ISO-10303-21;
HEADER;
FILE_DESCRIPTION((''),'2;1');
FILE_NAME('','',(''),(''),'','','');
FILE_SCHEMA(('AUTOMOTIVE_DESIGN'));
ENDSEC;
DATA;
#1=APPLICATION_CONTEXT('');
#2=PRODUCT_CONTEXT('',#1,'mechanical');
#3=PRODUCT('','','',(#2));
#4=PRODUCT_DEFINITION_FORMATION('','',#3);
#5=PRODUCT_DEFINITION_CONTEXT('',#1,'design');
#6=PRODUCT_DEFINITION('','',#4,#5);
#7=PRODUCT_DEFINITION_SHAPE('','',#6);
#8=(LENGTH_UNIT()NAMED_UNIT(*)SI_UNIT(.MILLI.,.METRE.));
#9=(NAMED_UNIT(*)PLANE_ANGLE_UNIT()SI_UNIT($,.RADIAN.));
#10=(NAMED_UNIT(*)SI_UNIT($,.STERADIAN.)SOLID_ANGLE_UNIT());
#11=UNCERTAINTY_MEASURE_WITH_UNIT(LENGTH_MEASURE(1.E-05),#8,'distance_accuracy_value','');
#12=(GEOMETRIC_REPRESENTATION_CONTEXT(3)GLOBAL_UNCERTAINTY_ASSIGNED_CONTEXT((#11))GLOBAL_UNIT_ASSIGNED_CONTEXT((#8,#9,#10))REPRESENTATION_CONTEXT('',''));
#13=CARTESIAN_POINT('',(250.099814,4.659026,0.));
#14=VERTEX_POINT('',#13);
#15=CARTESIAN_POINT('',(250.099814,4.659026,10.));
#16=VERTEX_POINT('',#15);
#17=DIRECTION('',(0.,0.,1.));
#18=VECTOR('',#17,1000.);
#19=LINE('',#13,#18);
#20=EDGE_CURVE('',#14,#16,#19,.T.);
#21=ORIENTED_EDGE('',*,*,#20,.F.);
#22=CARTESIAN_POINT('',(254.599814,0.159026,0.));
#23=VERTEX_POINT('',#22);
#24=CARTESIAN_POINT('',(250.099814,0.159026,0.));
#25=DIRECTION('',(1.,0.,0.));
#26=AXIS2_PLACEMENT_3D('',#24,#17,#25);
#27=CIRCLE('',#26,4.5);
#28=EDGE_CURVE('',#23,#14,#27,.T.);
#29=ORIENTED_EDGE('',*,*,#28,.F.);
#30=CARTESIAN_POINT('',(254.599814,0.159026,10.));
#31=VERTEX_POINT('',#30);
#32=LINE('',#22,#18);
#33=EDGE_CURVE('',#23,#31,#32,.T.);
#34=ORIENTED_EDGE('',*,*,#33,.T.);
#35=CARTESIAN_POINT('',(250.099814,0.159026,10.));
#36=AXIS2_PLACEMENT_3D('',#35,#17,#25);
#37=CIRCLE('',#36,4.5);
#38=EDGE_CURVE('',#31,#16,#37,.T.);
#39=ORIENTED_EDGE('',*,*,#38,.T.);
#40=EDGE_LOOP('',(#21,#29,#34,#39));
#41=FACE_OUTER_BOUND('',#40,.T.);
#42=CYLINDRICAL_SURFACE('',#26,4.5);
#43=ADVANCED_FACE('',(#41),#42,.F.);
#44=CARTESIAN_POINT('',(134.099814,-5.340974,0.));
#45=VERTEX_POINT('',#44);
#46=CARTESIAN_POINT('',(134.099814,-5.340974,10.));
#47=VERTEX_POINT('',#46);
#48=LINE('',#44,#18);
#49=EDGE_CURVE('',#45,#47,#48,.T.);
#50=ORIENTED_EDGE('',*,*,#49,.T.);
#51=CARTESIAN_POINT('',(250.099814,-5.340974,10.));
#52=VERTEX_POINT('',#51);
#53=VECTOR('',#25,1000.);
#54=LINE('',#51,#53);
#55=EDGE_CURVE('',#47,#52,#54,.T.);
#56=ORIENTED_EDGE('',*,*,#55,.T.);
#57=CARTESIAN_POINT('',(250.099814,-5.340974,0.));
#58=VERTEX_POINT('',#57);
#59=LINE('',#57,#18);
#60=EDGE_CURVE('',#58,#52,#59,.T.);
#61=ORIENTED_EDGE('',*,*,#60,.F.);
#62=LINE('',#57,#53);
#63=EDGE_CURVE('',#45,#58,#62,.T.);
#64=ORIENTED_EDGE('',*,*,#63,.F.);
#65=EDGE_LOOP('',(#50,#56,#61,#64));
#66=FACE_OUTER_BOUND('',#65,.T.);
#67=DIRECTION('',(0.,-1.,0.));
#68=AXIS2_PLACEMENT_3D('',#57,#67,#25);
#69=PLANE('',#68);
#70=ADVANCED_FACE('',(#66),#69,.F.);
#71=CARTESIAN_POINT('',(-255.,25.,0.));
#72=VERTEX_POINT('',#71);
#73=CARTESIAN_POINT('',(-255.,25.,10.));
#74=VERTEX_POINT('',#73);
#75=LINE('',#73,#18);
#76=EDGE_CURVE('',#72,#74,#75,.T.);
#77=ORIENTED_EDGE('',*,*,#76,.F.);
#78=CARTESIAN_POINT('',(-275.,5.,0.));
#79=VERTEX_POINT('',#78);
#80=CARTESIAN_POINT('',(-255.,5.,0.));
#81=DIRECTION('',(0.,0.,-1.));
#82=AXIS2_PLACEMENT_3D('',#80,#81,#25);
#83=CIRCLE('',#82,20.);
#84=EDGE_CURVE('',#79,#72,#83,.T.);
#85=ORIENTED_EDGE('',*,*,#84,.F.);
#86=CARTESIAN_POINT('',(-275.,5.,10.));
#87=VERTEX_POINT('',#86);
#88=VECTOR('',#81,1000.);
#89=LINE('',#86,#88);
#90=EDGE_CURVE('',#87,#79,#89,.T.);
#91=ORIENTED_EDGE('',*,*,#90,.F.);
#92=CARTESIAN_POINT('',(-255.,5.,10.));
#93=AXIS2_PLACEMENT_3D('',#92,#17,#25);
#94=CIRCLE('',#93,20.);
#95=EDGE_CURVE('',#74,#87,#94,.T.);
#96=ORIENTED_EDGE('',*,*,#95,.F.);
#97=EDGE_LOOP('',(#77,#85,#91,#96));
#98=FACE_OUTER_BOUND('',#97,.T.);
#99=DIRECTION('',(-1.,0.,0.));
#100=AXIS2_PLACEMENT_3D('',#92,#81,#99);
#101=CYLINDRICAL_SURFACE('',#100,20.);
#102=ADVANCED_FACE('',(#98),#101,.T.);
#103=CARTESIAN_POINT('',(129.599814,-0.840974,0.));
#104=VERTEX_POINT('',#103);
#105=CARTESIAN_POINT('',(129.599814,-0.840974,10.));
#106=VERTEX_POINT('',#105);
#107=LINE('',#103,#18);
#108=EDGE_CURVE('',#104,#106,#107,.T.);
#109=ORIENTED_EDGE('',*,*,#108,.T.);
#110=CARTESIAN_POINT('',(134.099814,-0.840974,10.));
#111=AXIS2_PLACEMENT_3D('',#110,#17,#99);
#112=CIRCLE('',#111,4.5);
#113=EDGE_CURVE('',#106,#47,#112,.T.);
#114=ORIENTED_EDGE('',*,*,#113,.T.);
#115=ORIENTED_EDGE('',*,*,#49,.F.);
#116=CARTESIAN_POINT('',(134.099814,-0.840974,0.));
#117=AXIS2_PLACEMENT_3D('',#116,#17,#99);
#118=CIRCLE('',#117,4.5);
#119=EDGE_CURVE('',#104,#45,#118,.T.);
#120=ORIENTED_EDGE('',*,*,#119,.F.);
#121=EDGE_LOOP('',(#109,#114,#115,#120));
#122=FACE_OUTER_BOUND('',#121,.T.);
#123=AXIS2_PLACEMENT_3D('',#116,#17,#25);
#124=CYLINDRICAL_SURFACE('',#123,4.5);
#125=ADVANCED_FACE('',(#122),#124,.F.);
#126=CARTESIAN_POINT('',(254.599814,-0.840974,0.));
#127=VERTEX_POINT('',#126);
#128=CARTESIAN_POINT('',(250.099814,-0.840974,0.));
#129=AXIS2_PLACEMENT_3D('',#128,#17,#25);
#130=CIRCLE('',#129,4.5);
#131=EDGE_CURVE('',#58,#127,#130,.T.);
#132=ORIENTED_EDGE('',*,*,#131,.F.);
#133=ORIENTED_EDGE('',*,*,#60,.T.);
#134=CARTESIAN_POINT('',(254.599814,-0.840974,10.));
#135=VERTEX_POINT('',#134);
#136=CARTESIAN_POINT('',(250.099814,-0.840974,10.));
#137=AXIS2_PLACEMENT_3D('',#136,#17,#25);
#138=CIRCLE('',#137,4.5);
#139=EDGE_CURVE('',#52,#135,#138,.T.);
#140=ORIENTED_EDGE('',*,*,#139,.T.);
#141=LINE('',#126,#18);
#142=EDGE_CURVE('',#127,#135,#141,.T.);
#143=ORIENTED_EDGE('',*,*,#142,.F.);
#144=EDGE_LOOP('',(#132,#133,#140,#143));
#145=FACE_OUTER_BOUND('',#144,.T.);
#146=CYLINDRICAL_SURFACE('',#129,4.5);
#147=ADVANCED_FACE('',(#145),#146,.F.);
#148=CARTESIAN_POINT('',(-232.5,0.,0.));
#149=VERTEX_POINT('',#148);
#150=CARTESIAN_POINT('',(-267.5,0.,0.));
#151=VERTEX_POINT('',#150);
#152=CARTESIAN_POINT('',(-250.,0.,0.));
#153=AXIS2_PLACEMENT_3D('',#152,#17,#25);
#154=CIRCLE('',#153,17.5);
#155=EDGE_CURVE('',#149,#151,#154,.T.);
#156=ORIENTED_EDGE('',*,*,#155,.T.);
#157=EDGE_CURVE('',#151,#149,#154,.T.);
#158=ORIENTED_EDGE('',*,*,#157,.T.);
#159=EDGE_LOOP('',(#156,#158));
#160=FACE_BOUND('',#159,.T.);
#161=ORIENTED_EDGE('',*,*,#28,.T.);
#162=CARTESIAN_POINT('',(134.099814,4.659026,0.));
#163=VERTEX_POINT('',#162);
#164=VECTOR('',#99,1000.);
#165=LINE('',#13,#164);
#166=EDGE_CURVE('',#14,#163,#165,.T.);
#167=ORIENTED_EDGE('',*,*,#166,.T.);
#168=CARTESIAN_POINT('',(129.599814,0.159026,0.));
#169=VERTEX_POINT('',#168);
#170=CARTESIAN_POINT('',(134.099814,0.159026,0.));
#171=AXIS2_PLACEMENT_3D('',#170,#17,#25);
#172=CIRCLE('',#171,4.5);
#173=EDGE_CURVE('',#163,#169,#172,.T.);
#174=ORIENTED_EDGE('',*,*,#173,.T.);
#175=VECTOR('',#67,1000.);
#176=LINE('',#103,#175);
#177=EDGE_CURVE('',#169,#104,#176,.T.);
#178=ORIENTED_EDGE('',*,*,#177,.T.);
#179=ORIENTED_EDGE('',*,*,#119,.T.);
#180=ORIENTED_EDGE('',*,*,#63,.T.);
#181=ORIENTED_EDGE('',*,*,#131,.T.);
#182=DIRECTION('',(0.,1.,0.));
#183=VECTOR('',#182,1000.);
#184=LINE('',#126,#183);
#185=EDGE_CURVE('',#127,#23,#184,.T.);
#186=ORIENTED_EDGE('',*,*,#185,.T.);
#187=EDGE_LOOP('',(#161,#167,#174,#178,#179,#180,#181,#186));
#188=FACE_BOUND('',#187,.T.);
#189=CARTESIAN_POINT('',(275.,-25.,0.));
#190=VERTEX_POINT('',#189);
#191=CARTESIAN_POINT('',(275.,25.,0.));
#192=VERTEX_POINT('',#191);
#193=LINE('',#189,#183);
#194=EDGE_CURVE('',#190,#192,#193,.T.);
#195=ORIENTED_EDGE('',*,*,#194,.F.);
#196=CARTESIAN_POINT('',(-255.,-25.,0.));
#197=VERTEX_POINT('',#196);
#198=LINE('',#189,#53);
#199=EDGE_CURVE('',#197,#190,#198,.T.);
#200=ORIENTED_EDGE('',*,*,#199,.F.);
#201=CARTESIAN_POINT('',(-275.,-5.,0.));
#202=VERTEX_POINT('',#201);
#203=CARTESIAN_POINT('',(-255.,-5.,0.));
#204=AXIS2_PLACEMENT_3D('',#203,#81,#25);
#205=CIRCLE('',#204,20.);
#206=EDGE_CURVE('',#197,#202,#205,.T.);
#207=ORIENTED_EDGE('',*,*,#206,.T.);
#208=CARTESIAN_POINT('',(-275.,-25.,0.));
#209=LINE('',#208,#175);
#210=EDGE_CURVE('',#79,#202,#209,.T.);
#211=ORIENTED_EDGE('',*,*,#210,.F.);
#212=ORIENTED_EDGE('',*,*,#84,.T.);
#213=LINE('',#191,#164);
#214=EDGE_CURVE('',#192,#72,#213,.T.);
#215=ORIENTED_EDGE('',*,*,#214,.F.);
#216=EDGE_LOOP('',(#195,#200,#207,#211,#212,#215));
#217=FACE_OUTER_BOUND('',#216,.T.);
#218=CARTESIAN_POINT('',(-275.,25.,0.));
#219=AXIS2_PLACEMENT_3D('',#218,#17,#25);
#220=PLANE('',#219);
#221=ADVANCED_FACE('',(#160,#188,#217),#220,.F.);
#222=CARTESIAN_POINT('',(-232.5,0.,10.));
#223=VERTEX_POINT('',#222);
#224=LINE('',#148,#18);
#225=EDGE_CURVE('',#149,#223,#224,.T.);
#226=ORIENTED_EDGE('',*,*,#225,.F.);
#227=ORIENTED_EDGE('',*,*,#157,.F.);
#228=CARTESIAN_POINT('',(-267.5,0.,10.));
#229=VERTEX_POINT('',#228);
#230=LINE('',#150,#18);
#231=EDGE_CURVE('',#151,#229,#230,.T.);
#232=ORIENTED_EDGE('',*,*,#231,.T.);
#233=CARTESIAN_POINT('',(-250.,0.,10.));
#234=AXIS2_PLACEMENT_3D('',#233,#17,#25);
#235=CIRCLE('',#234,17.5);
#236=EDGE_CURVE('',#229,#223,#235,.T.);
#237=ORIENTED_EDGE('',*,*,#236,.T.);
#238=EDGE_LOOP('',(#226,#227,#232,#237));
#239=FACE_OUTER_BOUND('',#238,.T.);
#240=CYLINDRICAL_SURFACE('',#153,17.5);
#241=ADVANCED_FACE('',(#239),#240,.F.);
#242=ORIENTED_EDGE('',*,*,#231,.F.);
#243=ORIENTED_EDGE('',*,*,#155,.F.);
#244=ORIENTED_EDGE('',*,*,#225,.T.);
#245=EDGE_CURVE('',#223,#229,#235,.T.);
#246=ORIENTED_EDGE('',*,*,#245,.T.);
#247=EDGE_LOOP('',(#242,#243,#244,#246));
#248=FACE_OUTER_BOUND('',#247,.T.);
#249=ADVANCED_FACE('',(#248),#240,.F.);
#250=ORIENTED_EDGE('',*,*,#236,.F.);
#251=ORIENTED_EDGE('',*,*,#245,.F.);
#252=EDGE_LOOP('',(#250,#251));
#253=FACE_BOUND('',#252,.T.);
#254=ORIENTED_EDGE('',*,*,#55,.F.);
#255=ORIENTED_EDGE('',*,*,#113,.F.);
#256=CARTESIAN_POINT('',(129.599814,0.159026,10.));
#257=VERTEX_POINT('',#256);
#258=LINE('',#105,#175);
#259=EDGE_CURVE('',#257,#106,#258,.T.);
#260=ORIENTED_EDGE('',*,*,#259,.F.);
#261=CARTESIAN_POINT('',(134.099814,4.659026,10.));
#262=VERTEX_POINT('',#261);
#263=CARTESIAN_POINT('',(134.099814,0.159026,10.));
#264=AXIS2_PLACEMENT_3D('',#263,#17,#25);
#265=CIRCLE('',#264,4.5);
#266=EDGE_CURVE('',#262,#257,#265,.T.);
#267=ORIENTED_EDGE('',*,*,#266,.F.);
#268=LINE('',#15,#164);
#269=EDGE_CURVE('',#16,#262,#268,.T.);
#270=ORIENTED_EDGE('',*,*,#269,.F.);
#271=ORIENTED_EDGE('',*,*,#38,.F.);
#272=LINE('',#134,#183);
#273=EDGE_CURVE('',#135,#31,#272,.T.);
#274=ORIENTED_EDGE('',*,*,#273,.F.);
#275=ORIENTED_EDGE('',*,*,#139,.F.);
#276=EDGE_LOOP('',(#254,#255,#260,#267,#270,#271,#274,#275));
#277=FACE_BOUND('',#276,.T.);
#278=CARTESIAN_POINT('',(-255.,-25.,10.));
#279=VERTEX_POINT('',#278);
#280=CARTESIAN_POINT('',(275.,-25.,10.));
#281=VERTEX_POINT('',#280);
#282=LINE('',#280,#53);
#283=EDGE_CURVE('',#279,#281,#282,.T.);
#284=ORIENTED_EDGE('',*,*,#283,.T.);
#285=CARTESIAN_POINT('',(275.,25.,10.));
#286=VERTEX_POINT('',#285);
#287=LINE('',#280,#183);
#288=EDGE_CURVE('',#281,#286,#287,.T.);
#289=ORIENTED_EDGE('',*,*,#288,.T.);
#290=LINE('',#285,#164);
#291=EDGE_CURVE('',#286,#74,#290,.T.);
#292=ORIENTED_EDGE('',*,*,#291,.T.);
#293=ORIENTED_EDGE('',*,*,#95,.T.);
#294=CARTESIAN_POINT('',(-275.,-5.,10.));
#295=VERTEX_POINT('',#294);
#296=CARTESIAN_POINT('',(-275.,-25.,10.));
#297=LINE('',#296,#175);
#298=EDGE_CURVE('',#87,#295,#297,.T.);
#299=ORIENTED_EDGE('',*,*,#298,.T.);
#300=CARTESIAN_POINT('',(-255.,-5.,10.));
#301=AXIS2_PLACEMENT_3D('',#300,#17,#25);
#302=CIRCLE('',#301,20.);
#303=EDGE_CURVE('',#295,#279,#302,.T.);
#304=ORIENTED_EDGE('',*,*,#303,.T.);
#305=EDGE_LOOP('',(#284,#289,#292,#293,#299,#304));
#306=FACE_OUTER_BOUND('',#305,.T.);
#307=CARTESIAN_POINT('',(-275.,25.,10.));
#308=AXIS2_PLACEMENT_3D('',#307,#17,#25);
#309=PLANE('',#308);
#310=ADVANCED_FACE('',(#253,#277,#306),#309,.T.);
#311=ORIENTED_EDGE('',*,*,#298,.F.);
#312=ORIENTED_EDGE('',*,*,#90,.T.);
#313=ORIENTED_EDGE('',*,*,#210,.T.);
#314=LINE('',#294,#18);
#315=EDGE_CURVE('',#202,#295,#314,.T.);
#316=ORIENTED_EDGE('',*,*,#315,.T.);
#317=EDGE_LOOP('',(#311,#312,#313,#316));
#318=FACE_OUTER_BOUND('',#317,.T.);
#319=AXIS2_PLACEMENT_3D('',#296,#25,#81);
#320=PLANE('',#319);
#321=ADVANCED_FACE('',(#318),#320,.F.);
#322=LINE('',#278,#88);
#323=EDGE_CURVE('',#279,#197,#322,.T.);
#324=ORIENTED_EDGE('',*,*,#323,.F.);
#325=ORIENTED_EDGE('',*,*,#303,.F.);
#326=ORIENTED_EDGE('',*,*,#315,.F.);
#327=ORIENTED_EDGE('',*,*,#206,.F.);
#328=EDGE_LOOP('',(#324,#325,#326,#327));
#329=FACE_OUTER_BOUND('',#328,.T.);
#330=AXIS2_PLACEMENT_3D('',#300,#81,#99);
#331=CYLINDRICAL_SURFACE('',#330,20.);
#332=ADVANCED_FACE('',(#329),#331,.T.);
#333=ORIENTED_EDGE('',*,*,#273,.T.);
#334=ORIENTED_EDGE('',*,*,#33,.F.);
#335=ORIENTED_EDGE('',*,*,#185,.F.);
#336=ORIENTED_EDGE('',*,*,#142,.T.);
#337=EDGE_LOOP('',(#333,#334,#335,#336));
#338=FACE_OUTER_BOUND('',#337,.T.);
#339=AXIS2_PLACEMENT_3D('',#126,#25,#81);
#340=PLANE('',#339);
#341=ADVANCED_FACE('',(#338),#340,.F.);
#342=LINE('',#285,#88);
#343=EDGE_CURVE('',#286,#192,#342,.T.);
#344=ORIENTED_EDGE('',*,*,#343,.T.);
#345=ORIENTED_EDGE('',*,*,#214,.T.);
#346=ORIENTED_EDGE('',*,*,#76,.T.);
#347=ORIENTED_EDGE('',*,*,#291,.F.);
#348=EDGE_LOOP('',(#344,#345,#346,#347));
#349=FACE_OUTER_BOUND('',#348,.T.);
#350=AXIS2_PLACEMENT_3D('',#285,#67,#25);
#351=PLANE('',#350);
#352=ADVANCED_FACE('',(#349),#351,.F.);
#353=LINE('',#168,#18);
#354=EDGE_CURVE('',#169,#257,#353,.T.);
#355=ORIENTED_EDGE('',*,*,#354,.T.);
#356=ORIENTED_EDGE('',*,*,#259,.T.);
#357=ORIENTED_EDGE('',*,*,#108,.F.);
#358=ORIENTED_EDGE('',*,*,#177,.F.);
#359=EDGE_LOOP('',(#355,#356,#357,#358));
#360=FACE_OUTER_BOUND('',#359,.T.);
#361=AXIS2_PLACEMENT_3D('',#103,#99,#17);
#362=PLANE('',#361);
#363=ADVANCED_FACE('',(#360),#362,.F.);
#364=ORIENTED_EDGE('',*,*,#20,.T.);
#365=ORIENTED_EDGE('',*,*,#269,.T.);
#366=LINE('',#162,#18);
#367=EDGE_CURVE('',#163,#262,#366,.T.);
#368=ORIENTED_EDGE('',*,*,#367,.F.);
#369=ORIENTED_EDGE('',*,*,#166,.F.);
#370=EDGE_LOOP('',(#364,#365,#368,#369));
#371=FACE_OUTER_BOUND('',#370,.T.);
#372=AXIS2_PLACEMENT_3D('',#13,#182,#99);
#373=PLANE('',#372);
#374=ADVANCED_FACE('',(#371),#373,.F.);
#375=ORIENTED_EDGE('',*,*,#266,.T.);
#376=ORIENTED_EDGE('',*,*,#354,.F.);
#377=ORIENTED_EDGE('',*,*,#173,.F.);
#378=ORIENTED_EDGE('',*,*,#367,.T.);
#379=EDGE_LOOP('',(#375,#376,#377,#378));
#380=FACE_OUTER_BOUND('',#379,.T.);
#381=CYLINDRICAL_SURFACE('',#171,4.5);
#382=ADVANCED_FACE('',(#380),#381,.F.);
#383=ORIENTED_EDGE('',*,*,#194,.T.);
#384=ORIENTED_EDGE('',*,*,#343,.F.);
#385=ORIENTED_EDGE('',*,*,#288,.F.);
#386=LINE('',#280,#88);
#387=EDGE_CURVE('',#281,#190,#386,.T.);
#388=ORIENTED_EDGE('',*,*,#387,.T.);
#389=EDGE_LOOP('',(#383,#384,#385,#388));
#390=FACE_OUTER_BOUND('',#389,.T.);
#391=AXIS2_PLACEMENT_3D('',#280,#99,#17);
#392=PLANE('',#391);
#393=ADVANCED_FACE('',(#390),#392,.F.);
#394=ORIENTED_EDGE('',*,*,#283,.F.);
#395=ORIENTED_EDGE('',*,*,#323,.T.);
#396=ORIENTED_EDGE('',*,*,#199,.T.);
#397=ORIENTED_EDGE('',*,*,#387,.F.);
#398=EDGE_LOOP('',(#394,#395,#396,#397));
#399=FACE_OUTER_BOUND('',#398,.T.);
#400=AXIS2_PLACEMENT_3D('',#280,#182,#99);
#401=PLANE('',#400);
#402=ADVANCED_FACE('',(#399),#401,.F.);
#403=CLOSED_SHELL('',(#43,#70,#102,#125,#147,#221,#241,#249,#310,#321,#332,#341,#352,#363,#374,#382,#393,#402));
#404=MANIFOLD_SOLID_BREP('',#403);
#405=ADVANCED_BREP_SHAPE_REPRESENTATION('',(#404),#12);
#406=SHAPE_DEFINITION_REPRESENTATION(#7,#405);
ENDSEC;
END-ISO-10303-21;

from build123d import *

# Parameters (mm, degrees)
SKETCH1_W           = 550
SKETCH1_H           = 50
BOSS_EXTRUDE1_DEPTH = 10
SKETCH2_R           = 17.5
CUT_EXTRUDE1_DEPTH  = 10
CUT_EXTRUDE2_DEPTH  = 10
FILLET1_R           = 20


with BuildPart() as part:
    # Sketch1 → Boss-Extrude1 (new body)
    with BuildSketch(Plane.XY):
        Rectangle(SKETCH1_W, SKETCH1_H)
    extrude(amount=BOSS_EXTRUDE1_DEPTH)

    # Sketch2 → Cut-Extrude1 (cut)
    with BuildSketch(Plane.XY.offset(10)):
        with Locations((-250, 0)):
            Circle(SKETCH2_R)
    extrude(amount=-CUT_EXTRUDE1_DEPTH, mode=Mode.SUBTRACT)

    # Sketch3 → Cut-Extrude2 (cut)
    with BuildSketch(Plane.XY.offset(10)):
        with BuildLine():
            Line((250.099813904, -5.340973555), (134.099813904, -5.340973555))
            ThreePointArc((134.099813904, -5.340973555), (130.917833389, -4.02295407), (129.599813904, -0.840973555))
            Line((129.599813904, -0.840973555), (129.599813904, 0.159026445))
            ThreePointArc((129.599813904, 0.159026445), (130.917833389, 3.341006961), (134.099813904, 4.659026445))
            Line((134.099813904, 4.659026445), (250.099813904, 4.659026445))
            ThreePointArc((250.099813904, 4.659026445), (253.281794419, 3.341006961), (254.599813904, 0.159026445))
            Line((254.599813904, 0.159026445), (254.599813904, -0.840973555))
            ThreePointArc((254.599813904, -0.840973555), (253.281794419, -4.02295407), (250.099813904, -5.340973555))
        make_face()
    extrude(amount=-CUT_EXTRUDE2_DEPTH, mode=Mode.SUBTRACT)

    # Fillet1
    fillet1_edges = [part.edges().sort_by_distance(p)[0] for p in [
        (-275, 25, 5),
        (-275, -25, 5),
    ]]
    fillet(fillet1_edges, radius=FILLET1_R)


solid = part.part
